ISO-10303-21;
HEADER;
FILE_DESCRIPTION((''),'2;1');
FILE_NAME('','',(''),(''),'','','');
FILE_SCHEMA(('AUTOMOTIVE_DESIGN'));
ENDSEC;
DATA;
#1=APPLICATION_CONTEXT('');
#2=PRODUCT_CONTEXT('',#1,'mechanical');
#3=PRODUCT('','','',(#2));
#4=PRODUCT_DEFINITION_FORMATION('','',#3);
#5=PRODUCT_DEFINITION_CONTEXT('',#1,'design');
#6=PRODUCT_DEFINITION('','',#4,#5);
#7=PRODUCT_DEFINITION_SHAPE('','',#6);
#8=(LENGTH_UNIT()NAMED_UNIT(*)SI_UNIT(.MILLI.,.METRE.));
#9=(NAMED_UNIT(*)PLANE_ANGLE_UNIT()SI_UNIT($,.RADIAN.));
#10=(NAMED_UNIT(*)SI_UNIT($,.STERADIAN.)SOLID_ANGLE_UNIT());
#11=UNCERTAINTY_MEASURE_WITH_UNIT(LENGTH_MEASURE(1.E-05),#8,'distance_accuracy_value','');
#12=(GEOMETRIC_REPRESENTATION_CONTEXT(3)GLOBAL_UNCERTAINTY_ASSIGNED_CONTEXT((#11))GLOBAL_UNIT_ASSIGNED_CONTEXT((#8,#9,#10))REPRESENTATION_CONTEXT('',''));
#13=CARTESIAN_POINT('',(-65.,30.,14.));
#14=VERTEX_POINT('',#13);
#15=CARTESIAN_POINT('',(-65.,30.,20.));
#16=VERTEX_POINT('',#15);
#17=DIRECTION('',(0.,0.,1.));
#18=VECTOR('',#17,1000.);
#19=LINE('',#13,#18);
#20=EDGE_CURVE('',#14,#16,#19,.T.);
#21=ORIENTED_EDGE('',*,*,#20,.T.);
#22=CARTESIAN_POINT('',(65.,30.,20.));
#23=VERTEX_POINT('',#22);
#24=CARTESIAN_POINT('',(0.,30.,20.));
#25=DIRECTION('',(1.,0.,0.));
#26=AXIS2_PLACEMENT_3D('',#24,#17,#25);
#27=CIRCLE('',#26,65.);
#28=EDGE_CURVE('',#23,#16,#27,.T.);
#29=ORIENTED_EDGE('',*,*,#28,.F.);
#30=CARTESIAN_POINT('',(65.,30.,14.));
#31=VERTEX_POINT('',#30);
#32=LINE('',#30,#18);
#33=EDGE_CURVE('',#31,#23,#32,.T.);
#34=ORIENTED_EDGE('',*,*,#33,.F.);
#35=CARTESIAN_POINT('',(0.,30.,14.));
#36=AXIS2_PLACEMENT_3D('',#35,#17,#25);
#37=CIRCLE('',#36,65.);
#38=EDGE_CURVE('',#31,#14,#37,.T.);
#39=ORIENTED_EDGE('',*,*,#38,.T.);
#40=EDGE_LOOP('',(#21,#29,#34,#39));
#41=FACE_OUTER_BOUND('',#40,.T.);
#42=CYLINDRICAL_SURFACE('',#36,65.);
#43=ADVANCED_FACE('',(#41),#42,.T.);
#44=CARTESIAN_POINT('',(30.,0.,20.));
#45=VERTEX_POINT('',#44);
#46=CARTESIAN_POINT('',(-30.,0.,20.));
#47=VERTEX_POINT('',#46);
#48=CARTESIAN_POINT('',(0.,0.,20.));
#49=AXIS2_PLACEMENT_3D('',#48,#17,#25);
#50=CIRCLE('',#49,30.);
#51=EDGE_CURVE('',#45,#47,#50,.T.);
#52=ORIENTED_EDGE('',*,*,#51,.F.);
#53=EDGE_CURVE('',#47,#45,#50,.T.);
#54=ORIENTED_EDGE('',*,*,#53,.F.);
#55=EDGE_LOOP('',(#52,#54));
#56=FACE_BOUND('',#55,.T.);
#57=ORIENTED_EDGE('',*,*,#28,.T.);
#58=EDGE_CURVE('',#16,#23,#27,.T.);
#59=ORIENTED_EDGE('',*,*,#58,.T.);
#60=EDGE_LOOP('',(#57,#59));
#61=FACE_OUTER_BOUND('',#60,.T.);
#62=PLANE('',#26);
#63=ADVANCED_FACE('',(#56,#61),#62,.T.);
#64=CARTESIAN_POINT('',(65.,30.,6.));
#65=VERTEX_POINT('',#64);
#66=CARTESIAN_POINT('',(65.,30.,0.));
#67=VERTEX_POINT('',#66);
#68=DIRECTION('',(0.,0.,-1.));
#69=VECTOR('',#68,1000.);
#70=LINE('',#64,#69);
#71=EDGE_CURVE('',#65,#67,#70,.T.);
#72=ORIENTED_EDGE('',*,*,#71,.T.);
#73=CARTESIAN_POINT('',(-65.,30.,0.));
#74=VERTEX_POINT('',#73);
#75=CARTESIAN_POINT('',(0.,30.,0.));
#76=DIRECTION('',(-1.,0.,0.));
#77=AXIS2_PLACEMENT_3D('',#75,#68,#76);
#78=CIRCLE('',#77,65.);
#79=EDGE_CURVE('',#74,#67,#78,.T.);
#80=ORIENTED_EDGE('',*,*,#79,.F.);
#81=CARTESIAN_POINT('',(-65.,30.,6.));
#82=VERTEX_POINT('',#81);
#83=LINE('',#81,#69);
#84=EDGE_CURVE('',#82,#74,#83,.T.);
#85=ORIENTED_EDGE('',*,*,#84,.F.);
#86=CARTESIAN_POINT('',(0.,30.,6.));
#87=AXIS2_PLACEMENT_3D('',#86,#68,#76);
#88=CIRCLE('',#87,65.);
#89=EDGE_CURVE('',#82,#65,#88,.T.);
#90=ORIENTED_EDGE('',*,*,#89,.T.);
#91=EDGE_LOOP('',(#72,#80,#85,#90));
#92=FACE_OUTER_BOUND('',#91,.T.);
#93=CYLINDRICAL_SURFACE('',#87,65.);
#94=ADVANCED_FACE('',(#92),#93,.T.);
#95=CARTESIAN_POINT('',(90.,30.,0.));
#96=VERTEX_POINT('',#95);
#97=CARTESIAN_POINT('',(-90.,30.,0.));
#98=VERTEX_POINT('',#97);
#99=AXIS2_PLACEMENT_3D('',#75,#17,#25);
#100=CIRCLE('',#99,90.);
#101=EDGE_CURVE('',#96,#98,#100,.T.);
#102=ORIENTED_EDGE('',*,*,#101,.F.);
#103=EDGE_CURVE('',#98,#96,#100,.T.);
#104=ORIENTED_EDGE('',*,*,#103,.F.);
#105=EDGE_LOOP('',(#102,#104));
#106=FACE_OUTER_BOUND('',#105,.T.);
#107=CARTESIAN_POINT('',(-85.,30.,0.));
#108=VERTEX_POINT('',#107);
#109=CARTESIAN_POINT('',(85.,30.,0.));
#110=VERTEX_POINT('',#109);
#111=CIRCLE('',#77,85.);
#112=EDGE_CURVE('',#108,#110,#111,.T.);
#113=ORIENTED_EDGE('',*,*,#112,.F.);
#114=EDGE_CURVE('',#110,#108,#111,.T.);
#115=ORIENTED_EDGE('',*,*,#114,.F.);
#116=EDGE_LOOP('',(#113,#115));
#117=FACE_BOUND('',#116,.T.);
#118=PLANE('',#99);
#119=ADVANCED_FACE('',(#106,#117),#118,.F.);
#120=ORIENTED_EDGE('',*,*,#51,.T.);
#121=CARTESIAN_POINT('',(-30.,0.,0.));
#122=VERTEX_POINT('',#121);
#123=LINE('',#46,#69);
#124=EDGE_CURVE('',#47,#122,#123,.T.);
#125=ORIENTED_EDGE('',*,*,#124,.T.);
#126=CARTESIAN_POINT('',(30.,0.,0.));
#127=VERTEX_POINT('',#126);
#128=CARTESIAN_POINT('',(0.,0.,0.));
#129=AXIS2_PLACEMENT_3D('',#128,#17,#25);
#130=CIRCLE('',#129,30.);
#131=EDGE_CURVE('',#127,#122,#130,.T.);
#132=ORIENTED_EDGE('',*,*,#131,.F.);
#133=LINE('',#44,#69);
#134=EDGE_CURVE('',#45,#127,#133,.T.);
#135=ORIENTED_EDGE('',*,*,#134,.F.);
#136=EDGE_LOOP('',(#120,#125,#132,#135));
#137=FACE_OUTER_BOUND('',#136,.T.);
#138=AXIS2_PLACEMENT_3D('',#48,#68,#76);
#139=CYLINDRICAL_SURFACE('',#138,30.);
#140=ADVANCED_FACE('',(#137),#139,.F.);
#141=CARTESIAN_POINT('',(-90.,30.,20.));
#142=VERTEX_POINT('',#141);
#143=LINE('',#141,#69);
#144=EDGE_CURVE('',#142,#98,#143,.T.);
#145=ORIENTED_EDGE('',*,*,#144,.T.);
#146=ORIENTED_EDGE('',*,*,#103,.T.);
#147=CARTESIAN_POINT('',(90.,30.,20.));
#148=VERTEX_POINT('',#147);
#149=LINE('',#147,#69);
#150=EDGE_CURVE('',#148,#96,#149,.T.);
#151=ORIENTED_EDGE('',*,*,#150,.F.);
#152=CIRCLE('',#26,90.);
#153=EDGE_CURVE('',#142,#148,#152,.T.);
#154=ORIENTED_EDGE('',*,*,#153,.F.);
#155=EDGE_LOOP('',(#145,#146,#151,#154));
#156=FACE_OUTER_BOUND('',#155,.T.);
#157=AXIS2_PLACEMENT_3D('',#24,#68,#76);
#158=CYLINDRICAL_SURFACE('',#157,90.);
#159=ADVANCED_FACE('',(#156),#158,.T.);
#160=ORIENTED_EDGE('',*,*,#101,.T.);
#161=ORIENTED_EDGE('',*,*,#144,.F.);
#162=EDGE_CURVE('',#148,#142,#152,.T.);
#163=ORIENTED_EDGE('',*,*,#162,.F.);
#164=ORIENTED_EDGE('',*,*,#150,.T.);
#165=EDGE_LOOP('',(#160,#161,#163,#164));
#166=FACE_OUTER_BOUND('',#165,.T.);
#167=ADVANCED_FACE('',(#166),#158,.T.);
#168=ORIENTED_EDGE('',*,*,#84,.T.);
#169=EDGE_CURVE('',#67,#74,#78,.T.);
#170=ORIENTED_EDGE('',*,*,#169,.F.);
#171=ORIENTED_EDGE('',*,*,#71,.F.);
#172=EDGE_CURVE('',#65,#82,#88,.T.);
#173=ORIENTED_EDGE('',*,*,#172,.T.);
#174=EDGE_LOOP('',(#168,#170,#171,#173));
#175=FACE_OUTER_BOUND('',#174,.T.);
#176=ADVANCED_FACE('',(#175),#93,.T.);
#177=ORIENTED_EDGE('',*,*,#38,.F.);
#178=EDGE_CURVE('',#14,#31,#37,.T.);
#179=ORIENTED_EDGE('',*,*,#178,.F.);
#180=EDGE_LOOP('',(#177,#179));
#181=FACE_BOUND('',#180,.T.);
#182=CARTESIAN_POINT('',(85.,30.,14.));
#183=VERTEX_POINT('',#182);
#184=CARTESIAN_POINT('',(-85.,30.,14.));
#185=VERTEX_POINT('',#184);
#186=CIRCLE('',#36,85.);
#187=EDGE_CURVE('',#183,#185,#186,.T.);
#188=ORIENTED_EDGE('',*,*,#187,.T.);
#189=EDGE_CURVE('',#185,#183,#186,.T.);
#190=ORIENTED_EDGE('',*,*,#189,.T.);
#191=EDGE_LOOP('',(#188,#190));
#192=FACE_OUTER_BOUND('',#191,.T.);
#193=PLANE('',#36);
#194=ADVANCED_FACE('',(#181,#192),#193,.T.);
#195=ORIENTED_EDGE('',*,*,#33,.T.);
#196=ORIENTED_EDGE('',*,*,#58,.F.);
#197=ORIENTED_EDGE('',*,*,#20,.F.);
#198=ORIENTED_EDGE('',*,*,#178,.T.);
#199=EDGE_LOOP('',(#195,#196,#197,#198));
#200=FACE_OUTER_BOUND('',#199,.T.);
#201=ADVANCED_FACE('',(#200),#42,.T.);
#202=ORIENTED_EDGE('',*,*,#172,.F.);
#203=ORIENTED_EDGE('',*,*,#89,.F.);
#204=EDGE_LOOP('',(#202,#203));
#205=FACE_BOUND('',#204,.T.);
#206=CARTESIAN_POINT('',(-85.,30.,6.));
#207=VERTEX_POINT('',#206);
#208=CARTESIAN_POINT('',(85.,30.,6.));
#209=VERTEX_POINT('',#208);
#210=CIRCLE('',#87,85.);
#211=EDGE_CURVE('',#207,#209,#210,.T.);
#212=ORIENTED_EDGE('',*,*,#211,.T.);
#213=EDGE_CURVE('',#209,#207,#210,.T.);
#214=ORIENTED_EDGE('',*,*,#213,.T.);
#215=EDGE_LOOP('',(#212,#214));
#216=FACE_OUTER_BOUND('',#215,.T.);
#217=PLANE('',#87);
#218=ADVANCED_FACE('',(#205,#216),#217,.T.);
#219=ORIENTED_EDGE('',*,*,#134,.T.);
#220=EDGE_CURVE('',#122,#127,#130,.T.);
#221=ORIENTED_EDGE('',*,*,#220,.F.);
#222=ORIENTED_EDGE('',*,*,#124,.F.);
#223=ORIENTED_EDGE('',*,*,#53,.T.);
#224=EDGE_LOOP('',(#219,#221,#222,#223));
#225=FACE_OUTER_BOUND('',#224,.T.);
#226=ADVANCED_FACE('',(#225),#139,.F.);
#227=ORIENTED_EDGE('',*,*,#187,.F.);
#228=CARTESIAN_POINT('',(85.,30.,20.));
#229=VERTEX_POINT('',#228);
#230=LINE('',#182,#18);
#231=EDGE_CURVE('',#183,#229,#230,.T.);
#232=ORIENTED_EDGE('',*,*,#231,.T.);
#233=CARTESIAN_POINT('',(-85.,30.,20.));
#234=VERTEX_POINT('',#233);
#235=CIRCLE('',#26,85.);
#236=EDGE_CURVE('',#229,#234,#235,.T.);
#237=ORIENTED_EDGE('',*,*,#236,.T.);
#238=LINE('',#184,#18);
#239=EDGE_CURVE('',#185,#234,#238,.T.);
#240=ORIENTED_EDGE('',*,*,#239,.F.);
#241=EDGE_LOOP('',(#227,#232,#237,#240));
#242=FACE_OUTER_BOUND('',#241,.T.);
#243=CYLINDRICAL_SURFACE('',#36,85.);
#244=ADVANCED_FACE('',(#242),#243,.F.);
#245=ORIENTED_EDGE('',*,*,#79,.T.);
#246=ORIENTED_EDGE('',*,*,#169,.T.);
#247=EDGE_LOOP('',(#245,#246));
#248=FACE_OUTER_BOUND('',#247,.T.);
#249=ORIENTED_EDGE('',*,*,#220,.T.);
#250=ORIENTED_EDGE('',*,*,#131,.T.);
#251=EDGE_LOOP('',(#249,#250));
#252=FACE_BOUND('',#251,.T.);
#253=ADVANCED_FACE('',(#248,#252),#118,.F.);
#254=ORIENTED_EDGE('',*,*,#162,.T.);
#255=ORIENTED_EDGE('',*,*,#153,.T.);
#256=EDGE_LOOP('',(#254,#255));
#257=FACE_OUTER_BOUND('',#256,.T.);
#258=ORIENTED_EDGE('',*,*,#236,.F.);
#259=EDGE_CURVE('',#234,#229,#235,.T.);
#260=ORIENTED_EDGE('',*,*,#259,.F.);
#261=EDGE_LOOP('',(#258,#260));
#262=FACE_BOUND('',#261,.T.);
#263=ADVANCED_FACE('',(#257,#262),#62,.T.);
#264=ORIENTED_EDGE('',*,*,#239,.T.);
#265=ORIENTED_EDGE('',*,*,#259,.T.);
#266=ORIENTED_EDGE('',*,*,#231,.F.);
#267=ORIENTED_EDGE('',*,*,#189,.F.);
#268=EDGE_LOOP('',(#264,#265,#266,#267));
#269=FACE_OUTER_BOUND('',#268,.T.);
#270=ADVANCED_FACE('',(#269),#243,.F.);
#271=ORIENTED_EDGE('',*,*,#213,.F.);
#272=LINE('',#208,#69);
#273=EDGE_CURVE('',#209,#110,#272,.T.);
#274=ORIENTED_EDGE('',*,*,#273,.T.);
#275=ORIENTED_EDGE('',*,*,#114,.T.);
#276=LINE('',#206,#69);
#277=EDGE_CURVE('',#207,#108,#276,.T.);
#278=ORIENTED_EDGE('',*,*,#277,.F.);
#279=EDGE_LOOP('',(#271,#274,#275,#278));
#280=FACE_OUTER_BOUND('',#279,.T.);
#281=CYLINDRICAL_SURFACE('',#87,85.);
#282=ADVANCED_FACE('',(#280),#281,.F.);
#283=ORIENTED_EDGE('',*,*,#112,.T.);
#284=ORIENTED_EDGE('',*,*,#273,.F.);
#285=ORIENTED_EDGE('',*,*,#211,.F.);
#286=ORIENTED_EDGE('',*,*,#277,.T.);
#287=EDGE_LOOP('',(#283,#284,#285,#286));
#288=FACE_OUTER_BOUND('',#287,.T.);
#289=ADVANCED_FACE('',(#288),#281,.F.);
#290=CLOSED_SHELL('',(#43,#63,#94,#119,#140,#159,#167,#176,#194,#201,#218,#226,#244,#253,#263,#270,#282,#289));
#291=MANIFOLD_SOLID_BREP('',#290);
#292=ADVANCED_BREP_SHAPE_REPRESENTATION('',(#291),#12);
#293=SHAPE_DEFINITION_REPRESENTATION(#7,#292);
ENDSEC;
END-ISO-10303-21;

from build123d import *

# Parameters (mm, degrees)
SKETCH1_R           = 90
SKETCH1_R_2         = 30
BOSS_EXTRUDE1_DEPTH = 20
SKETCH2_R           = 85
SKETCH2_R_2         = 65
CUT_EXTRUDE1_DEPTH  = 6
CUT_EXTRUDE2_START  = -6
SKETCH3_R           = 85
SKETCH3_R_2         = 65
CUT_EXTRUDE2_DEPTH  = 6


with BuildPart() as part:
    # Sketch1 → Boss-Extrude1 (new body)
    with BuildSketch(Plane.XY):
        with Locations((0, 30)):
            Circle(SKETCH1_R)
        Circle(SKETCH1_R_2, mode=Mode.SUBTRACT)
    extrude(amount=BOSS_EXTRUDE1_DEPTH)

    # Sketch2 → Cut-Extrude1 (cut)
    with BuildSketch(Plane.XY.offset(20)):
        with Locations((0, 30)):
            Circle(SKETCH2_R)
        with Locations((0, 30)):
            Circle(SKETCH2_R_2, mode=Mode.SUBTRACT)
    extrude(amount=-CUT_EXTRUDE1_DEPTH, mode=Mode.SUBTRACT)

    # Sketch3 → Cut-Extrude2 (cut)
    with BuildSketch(Plane(origin=(0, 0, 0), x_dir=(-1, 0, 0), z_dir=(0, 0, -1)).offset(CUT_EXTRUDE2_START)):
        with Locations(Location((0, 30, 0), (0, 0, 180))):
            Circle(SKETCH3_R)
        with Locations(Location((0, 30, 0), (0, 0, 180))):
            Circle(SKETCH3_R_2, mode=Mode.SUBTRACT)
    extrude(amount=CUT_EXTRUDE2_DEPTH, mode=Mode.SUBTRACT)


solid = part.part
